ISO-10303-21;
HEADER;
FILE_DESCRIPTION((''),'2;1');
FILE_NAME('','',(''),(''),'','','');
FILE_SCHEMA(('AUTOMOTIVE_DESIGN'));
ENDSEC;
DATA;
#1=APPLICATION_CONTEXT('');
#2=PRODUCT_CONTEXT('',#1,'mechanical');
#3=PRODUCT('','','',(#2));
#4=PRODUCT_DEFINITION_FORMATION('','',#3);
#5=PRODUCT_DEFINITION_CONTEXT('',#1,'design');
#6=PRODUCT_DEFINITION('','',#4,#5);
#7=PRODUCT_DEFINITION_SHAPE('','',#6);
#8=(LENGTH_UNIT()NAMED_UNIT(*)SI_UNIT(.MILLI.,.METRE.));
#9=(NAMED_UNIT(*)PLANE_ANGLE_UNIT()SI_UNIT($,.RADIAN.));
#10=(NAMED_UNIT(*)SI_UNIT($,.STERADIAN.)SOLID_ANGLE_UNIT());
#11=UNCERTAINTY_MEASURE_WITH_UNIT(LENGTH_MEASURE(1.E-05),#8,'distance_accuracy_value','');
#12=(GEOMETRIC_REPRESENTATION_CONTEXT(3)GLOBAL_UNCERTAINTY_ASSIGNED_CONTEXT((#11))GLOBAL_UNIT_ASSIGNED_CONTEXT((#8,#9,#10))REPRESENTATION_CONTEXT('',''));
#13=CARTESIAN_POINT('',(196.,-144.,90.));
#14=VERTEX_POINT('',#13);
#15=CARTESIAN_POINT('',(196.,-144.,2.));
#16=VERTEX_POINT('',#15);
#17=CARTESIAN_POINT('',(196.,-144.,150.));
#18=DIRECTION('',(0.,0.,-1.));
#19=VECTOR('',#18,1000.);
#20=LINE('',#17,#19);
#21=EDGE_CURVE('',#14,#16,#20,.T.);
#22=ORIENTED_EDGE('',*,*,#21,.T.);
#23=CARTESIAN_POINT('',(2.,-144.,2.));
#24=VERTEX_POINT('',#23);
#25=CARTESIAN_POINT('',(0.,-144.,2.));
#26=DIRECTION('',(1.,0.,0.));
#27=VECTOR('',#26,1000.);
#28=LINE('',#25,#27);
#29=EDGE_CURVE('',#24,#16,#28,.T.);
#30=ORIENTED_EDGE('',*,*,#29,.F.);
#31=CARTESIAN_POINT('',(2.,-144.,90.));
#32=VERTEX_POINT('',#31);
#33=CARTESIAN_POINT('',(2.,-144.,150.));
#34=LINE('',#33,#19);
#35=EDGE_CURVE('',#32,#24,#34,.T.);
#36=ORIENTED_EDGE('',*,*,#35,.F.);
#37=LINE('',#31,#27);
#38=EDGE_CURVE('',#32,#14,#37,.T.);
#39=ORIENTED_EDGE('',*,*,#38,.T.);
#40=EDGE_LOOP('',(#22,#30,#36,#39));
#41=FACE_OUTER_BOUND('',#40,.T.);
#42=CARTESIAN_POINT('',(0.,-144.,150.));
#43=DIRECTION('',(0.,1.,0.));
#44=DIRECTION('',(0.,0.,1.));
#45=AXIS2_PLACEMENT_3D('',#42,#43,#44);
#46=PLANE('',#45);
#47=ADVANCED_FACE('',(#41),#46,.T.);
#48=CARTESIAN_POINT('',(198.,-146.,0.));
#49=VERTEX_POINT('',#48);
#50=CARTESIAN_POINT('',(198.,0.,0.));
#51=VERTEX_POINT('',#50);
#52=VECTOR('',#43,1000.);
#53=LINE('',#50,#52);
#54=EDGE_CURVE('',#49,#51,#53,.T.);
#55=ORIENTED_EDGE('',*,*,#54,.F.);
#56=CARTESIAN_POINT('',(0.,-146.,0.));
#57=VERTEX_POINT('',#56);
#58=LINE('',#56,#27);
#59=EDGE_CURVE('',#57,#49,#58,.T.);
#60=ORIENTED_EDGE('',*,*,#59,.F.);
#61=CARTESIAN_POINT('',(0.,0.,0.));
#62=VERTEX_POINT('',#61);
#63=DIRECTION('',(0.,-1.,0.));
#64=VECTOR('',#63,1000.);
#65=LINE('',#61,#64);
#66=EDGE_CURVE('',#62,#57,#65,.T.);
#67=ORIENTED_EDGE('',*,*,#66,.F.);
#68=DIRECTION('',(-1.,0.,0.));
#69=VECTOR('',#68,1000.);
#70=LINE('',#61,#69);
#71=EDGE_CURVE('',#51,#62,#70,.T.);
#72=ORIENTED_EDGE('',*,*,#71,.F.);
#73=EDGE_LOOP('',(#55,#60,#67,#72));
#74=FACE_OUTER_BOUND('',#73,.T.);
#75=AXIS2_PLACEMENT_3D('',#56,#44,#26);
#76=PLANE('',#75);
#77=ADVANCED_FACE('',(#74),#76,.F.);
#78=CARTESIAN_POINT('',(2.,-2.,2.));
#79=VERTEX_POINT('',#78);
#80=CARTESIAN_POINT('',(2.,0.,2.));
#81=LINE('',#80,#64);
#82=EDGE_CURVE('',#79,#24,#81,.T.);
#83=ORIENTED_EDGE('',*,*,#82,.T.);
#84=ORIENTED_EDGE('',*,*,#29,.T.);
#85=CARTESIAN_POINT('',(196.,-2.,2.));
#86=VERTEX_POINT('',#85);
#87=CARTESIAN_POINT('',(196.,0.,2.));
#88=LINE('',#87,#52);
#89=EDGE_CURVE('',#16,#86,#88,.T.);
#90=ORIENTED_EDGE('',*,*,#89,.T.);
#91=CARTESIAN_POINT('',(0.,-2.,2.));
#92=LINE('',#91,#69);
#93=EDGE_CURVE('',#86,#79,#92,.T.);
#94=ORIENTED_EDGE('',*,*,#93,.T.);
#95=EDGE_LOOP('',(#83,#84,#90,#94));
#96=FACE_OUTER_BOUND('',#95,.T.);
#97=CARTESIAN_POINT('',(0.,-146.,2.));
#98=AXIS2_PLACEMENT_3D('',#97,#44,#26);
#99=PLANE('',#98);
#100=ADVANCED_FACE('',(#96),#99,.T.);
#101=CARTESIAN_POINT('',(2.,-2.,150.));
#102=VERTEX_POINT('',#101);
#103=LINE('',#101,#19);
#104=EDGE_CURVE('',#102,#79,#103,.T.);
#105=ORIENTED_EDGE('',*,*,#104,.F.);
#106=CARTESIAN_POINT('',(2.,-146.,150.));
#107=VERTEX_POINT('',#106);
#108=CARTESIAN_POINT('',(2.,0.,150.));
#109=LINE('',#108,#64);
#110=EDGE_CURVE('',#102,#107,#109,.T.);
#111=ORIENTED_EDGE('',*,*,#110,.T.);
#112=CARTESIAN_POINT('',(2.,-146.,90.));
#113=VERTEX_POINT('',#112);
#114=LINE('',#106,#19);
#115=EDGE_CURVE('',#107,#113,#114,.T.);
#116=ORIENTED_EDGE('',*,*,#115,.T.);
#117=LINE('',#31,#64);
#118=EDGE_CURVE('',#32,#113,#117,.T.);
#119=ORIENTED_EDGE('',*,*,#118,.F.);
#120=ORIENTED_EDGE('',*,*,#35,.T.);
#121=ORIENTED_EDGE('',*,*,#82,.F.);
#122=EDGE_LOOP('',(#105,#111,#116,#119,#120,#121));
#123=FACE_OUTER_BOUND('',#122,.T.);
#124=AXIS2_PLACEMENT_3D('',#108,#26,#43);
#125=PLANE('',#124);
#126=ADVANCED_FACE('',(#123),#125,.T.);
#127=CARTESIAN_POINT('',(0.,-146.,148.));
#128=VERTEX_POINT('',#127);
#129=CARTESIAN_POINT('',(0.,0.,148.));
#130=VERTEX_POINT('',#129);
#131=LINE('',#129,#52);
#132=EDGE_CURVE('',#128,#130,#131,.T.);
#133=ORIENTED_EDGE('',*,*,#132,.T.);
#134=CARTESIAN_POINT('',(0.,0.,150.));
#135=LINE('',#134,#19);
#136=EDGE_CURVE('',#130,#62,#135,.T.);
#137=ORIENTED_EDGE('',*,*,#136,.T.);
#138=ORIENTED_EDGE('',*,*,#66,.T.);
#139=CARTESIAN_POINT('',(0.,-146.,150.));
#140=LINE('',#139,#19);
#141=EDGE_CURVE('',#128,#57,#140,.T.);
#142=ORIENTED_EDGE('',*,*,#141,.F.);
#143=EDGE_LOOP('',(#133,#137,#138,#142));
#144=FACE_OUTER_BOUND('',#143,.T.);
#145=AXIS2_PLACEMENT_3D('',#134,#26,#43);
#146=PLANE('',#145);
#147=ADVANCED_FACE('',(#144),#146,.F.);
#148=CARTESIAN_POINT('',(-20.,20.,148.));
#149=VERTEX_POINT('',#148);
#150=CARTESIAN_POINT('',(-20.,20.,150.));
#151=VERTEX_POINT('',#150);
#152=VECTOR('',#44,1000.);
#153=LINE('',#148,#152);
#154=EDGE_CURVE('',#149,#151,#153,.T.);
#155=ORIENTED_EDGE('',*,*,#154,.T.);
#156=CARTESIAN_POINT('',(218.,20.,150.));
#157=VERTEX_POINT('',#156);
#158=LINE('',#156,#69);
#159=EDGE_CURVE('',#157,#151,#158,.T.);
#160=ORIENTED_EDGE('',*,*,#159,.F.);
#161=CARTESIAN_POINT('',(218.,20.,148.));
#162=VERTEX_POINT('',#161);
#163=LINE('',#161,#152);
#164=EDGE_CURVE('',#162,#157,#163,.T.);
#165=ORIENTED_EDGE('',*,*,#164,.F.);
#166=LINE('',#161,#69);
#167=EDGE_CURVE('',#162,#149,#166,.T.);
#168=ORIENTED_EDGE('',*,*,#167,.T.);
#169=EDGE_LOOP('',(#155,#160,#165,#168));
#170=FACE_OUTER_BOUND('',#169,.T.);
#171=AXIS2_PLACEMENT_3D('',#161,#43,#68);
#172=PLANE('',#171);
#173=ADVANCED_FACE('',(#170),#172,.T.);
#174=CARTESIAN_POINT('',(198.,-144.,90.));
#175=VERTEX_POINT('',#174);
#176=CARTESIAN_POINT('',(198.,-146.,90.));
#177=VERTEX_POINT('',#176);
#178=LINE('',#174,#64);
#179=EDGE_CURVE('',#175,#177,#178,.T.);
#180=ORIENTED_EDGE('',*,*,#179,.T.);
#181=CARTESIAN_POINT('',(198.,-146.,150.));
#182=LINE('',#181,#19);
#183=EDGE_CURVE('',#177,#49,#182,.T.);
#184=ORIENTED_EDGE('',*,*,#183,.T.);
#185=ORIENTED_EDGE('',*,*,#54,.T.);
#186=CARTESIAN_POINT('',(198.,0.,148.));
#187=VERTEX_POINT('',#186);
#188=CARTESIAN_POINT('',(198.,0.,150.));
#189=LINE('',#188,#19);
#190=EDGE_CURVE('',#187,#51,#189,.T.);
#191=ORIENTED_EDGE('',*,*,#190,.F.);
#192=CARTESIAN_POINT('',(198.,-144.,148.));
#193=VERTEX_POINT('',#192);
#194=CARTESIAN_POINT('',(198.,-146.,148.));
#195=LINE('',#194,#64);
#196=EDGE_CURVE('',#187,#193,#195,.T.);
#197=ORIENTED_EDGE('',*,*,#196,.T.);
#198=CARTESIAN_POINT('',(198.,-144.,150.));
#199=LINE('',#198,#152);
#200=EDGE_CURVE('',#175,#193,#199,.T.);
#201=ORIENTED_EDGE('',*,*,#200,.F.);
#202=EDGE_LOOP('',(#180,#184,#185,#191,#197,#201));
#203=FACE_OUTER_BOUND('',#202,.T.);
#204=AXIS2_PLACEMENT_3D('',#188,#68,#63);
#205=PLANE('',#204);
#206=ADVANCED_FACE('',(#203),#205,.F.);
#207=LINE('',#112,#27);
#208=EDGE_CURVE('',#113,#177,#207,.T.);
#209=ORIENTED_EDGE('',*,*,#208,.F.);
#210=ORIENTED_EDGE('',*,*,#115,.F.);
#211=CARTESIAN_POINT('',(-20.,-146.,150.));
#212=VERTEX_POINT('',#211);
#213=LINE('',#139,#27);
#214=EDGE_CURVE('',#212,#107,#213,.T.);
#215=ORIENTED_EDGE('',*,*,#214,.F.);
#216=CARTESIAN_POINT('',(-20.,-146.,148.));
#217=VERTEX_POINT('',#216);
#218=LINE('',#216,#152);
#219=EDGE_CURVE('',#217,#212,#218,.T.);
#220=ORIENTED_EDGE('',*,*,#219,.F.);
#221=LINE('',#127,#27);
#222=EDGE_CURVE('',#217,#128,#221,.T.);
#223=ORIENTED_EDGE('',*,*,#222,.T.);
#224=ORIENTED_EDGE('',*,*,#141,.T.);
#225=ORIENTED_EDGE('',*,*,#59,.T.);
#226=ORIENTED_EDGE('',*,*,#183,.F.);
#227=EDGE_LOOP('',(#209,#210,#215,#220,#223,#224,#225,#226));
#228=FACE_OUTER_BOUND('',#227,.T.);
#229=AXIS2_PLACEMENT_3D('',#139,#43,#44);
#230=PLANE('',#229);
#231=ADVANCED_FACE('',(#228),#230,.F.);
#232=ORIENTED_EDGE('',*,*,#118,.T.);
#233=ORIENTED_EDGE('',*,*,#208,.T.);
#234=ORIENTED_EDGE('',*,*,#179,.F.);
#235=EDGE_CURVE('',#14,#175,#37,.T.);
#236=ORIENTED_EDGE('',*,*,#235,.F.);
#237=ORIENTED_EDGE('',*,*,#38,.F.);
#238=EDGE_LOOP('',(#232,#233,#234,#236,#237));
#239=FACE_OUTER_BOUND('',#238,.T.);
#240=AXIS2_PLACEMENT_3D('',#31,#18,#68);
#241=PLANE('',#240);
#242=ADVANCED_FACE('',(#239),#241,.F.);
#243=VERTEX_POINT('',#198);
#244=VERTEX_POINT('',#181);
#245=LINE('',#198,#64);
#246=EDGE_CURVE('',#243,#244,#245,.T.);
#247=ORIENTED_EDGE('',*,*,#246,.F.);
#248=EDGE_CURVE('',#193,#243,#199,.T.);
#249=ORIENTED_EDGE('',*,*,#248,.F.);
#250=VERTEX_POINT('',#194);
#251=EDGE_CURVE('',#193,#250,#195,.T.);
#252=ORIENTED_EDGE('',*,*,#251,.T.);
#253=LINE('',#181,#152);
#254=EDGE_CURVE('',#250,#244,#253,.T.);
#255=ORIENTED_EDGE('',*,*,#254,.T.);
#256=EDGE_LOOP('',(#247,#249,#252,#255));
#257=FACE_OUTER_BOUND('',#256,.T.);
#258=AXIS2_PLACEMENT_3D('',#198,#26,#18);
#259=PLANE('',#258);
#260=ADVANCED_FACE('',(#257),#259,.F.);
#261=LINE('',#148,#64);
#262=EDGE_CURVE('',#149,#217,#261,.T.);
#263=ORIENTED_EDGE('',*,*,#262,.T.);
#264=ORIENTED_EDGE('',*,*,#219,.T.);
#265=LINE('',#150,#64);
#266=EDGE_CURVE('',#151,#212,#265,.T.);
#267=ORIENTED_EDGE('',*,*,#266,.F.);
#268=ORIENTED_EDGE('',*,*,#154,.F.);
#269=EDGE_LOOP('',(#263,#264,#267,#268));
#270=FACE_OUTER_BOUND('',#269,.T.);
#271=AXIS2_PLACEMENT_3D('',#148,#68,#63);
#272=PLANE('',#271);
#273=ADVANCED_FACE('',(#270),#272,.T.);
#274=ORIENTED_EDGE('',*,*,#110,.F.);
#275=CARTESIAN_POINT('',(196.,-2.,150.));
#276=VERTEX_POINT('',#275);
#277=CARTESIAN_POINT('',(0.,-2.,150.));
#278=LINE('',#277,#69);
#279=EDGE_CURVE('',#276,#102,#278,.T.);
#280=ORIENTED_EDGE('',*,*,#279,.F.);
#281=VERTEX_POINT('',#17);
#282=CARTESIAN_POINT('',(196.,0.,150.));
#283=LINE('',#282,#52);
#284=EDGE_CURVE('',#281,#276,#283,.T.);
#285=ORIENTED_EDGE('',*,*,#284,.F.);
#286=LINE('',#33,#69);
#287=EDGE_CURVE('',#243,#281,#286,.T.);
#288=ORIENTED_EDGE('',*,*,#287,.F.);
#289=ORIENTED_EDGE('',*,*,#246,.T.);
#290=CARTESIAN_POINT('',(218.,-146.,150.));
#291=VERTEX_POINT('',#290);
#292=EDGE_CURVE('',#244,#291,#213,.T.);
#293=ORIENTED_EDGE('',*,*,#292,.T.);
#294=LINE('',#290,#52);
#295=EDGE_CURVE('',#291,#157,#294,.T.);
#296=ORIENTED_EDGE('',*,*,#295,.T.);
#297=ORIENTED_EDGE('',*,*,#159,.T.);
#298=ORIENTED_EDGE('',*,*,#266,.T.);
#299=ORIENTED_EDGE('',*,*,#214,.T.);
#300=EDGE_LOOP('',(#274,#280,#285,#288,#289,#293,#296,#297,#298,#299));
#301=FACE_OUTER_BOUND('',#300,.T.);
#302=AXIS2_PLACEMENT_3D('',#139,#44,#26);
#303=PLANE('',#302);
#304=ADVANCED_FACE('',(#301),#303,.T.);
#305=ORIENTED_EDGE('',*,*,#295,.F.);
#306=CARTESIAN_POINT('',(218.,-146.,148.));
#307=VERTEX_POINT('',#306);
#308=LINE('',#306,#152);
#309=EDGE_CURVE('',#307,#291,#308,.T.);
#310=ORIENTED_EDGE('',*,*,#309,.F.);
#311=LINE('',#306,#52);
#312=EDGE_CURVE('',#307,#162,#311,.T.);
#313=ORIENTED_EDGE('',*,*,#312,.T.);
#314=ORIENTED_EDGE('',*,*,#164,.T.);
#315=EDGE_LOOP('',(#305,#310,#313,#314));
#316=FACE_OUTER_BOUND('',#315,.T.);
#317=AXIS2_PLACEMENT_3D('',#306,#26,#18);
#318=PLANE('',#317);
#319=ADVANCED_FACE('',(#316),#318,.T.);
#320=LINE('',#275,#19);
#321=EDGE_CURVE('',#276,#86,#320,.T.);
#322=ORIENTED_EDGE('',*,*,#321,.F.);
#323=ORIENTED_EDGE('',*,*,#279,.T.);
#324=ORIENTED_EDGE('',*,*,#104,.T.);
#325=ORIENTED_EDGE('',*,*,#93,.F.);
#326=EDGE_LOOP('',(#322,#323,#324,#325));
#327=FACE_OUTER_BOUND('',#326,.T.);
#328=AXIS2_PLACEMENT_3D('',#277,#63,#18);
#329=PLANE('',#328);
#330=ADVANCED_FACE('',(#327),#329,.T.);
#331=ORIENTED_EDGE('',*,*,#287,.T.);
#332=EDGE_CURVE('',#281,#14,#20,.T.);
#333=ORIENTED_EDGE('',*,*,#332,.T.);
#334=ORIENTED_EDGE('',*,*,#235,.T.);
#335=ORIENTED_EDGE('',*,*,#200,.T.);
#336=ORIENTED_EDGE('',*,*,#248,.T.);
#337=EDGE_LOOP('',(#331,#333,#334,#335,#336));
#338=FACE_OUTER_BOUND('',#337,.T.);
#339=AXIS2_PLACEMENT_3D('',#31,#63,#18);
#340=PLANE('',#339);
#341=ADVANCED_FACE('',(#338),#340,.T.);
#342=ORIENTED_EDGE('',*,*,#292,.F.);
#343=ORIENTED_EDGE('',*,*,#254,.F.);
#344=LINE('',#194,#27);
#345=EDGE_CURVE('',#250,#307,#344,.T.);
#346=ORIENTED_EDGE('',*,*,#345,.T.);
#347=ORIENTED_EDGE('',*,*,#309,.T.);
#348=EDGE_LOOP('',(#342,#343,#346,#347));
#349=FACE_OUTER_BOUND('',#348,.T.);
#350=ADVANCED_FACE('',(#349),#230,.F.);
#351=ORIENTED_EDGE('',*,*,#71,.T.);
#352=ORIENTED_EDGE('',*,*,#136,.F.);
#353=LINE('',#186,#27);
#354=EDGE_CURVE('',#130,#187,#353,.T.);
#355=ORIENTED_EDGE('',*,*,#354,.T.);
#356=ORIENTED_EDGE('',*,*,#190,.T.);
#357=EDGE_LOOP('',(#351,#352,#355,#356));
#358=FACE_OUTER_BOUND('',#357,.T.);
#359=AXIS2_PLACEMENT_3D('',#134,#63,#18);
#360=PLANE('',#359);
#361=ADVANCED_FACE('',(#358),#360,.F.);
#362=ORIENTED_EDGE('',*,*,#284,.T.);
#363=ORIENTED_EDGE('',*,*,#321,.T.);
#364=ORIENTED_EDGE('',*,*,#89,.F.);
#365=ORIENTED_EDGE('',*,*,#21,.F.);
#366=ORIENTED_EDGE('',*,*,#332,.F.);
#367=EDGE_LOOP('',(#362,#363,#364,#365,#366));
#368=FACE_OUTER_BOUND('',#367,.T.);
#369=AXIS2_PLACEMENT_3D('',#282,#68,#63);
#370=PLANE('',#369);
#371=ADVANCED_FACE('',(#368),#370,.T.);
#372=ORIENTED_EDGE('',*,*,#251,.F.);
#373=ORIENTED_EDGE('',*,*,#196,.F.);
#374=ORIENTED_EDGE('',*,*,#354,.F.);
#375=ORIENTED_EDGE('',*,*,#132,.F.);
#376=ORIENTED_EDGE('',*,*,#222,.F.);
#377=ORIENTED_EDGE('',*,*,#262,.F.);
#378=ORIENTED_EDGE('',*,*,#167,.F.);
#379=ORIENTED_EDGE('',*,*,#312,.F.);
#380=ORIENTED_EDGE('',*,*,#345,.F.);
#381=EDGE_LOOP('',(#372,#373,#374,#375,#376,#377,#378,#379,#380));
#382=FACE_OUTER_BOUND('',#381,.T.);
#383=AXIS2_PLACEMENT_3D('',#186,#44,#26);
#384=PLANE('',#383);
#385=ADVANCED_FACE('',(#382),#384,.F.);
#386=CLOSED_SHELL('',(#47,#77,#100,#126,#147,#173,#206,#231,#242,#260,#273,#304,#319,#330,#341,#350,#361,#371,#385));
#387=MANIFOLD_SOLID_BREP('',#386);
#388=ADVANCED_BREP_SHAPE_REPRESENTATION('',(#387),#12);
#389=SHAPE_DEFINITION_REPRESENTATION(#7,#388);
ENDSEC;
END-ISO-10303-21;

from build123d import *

# Parameters (mm, degrees)
SKETCH_1_W          = 198
SKETCH_1_H          = 146
EXTRUDE_1_DEPTH     = 150
SHELL_1_T           = -2
EXTRUDE_2_DEPTH     = 2
SKETCH_3_W          = 196
SKETCH_3_H          = 60
CUT_EXTRUDE_1_DEPTH = 2


with BuildPart() as part:
    # 草图1 → 凸台-拉伸1 (new body)
    with BuildSketch(Plane.XY):
        with Locations((99, -73)):
            Rectangle(SKETCH_1_W, SKETCH_1_H)
    extrude(amount=EXTRUDE_1_DEPTH)

    # 抽壳1
    shell_1_openings = [part.faces().sort_by_distance(p)[0] for p in [
        (99, -73, 150),
    ]]
    offset(amount=SHELL_1_T, openings=shell_1_openings, kind=Kind.INTERSECTION)

    # 草图2 → 凸台-拉伸2 (add)
    with BuildSketch(Plane.XY.offset(150)):
        Polygon((0, -146), (-20, -146), (-20, 20), (218, 20), (218, -146), (198, -146), (198, 0), (0, 0), align=None)
    extrude(amount=-EXTRUDE_2_DEPTH)

    # 草图3 → 切除-拉伸1 (cut)
    with BuildSketch(Plane.XZ.offset(146)):
        with Locations((100, 120)):
            Rectangle(SKETCH_3_W, SKETCH_3_H)
    extrude(amount=-CUT_EXTRUDE_1_DEPTH, mode=Mode.SUBTRACT)


solid = part.part
